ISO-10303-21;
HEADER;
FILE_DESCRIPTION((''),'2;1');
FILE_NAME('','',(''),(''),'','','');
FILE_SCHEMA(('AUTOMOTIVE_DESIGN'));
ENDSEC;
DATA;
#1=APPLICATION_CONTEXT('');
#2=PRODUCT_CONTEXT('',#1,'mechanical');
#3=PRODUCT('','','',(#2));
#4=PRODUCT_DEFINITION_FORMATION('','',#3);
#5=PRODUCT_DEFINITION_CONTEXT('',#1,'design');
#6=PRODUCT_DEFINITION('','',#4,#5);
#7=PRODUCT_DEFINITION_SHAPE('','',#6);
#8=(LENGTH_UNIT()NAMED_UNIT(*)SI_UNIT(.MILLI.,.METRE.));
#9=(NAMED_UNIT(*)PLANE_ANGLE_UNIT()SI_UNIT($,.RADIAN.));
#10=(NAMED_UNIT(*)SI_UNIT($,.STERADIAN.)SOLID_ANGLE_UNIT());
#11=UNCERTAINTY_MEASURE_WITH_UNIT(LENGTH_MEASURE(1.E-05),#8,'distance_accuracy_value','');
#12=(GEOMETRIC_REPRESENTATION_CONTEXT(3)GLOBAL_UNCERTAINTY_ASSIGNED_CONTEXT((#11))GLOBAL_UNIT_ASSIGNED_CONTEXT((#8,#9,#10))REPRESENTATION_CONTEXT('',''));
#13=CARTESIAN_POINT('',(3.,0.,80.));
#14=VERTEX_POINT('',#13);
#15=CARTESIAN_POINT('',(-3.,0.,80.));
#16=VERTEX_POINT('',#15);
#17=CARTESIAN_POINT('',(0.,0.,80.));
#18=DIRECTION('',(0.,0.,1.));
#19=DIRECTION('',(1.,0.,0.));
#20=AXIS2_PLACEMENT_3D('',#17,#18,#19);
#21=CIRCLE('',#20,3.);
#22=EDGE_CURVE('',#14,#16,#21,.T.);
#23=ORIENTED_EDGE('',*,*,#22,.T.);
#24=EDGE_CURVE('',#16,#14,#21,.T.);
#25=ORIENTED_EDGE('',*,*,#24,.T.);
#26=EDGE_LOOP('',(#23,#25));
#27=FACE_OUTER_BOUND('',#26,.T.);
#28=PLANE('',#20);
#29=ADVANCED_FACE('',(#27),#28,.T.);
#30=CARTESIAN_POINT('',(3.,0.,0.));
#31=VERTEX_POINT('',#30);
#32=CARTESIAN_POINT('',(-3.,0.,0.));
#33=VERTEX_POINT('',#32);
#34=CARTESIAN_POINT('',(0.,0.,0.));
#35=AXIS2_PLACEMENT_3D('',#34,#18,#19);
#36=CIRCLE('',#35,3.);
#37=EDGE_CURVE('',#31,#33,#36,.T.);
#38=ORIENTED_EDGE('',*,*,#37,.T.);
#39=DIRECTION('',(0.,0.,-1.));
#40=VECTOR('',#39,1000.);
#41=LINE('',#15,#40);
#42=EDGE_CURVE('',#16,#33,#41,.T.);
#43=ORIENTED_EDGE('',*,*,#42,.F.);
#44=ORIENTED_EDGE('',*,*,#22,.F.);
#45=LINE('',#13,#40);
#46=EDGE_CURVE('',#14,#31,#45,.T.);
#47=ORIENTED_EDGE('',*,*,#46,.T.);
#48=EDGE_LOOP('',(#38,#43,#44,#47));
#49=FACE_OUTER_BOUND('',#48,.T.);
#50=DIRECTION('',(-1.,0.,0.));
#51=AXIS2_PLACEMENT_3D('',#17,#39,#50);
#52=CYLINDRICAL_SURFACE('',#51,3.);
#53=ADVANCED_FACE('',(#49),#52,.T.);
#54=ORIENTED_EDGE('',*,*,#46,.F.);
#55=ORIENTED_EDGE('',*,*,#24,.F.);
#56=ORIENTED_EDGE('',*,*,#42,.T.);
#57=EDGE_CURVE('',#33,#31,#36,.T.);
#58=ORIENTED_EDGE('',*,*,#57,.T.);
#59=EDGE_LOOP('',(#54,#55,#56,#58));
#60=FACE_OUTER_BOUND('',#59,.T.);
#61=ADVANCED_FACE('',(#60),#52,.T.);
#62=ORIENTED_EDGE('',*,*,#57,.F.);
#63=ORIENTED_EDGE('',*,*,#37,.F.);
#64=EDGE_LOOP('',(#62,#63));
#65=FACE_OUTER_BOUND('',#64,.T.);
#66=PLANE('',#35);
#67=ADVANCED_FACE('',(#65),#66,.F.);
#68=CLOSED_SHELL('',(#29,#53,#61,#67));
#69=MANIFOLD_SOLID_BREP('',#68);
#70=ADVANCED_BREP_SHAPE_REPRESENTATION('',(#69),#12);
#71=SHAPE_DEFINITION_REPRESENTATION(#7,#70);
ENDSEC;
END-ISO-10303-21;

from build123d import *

# Parameters (mm, degrees)
SKETCH_1_R      = 3
EXTRUDE_1_DEPTH = 80


with BuildPart() as part:
    # 草图1 → 凸台-拉伸1 (new body)
    with BuildSketch(Plane.XY):
        Circle(SKETCH_1_R)
    extrude(amount=EXTRUDE_1_DEPTH)


solid = part.part
